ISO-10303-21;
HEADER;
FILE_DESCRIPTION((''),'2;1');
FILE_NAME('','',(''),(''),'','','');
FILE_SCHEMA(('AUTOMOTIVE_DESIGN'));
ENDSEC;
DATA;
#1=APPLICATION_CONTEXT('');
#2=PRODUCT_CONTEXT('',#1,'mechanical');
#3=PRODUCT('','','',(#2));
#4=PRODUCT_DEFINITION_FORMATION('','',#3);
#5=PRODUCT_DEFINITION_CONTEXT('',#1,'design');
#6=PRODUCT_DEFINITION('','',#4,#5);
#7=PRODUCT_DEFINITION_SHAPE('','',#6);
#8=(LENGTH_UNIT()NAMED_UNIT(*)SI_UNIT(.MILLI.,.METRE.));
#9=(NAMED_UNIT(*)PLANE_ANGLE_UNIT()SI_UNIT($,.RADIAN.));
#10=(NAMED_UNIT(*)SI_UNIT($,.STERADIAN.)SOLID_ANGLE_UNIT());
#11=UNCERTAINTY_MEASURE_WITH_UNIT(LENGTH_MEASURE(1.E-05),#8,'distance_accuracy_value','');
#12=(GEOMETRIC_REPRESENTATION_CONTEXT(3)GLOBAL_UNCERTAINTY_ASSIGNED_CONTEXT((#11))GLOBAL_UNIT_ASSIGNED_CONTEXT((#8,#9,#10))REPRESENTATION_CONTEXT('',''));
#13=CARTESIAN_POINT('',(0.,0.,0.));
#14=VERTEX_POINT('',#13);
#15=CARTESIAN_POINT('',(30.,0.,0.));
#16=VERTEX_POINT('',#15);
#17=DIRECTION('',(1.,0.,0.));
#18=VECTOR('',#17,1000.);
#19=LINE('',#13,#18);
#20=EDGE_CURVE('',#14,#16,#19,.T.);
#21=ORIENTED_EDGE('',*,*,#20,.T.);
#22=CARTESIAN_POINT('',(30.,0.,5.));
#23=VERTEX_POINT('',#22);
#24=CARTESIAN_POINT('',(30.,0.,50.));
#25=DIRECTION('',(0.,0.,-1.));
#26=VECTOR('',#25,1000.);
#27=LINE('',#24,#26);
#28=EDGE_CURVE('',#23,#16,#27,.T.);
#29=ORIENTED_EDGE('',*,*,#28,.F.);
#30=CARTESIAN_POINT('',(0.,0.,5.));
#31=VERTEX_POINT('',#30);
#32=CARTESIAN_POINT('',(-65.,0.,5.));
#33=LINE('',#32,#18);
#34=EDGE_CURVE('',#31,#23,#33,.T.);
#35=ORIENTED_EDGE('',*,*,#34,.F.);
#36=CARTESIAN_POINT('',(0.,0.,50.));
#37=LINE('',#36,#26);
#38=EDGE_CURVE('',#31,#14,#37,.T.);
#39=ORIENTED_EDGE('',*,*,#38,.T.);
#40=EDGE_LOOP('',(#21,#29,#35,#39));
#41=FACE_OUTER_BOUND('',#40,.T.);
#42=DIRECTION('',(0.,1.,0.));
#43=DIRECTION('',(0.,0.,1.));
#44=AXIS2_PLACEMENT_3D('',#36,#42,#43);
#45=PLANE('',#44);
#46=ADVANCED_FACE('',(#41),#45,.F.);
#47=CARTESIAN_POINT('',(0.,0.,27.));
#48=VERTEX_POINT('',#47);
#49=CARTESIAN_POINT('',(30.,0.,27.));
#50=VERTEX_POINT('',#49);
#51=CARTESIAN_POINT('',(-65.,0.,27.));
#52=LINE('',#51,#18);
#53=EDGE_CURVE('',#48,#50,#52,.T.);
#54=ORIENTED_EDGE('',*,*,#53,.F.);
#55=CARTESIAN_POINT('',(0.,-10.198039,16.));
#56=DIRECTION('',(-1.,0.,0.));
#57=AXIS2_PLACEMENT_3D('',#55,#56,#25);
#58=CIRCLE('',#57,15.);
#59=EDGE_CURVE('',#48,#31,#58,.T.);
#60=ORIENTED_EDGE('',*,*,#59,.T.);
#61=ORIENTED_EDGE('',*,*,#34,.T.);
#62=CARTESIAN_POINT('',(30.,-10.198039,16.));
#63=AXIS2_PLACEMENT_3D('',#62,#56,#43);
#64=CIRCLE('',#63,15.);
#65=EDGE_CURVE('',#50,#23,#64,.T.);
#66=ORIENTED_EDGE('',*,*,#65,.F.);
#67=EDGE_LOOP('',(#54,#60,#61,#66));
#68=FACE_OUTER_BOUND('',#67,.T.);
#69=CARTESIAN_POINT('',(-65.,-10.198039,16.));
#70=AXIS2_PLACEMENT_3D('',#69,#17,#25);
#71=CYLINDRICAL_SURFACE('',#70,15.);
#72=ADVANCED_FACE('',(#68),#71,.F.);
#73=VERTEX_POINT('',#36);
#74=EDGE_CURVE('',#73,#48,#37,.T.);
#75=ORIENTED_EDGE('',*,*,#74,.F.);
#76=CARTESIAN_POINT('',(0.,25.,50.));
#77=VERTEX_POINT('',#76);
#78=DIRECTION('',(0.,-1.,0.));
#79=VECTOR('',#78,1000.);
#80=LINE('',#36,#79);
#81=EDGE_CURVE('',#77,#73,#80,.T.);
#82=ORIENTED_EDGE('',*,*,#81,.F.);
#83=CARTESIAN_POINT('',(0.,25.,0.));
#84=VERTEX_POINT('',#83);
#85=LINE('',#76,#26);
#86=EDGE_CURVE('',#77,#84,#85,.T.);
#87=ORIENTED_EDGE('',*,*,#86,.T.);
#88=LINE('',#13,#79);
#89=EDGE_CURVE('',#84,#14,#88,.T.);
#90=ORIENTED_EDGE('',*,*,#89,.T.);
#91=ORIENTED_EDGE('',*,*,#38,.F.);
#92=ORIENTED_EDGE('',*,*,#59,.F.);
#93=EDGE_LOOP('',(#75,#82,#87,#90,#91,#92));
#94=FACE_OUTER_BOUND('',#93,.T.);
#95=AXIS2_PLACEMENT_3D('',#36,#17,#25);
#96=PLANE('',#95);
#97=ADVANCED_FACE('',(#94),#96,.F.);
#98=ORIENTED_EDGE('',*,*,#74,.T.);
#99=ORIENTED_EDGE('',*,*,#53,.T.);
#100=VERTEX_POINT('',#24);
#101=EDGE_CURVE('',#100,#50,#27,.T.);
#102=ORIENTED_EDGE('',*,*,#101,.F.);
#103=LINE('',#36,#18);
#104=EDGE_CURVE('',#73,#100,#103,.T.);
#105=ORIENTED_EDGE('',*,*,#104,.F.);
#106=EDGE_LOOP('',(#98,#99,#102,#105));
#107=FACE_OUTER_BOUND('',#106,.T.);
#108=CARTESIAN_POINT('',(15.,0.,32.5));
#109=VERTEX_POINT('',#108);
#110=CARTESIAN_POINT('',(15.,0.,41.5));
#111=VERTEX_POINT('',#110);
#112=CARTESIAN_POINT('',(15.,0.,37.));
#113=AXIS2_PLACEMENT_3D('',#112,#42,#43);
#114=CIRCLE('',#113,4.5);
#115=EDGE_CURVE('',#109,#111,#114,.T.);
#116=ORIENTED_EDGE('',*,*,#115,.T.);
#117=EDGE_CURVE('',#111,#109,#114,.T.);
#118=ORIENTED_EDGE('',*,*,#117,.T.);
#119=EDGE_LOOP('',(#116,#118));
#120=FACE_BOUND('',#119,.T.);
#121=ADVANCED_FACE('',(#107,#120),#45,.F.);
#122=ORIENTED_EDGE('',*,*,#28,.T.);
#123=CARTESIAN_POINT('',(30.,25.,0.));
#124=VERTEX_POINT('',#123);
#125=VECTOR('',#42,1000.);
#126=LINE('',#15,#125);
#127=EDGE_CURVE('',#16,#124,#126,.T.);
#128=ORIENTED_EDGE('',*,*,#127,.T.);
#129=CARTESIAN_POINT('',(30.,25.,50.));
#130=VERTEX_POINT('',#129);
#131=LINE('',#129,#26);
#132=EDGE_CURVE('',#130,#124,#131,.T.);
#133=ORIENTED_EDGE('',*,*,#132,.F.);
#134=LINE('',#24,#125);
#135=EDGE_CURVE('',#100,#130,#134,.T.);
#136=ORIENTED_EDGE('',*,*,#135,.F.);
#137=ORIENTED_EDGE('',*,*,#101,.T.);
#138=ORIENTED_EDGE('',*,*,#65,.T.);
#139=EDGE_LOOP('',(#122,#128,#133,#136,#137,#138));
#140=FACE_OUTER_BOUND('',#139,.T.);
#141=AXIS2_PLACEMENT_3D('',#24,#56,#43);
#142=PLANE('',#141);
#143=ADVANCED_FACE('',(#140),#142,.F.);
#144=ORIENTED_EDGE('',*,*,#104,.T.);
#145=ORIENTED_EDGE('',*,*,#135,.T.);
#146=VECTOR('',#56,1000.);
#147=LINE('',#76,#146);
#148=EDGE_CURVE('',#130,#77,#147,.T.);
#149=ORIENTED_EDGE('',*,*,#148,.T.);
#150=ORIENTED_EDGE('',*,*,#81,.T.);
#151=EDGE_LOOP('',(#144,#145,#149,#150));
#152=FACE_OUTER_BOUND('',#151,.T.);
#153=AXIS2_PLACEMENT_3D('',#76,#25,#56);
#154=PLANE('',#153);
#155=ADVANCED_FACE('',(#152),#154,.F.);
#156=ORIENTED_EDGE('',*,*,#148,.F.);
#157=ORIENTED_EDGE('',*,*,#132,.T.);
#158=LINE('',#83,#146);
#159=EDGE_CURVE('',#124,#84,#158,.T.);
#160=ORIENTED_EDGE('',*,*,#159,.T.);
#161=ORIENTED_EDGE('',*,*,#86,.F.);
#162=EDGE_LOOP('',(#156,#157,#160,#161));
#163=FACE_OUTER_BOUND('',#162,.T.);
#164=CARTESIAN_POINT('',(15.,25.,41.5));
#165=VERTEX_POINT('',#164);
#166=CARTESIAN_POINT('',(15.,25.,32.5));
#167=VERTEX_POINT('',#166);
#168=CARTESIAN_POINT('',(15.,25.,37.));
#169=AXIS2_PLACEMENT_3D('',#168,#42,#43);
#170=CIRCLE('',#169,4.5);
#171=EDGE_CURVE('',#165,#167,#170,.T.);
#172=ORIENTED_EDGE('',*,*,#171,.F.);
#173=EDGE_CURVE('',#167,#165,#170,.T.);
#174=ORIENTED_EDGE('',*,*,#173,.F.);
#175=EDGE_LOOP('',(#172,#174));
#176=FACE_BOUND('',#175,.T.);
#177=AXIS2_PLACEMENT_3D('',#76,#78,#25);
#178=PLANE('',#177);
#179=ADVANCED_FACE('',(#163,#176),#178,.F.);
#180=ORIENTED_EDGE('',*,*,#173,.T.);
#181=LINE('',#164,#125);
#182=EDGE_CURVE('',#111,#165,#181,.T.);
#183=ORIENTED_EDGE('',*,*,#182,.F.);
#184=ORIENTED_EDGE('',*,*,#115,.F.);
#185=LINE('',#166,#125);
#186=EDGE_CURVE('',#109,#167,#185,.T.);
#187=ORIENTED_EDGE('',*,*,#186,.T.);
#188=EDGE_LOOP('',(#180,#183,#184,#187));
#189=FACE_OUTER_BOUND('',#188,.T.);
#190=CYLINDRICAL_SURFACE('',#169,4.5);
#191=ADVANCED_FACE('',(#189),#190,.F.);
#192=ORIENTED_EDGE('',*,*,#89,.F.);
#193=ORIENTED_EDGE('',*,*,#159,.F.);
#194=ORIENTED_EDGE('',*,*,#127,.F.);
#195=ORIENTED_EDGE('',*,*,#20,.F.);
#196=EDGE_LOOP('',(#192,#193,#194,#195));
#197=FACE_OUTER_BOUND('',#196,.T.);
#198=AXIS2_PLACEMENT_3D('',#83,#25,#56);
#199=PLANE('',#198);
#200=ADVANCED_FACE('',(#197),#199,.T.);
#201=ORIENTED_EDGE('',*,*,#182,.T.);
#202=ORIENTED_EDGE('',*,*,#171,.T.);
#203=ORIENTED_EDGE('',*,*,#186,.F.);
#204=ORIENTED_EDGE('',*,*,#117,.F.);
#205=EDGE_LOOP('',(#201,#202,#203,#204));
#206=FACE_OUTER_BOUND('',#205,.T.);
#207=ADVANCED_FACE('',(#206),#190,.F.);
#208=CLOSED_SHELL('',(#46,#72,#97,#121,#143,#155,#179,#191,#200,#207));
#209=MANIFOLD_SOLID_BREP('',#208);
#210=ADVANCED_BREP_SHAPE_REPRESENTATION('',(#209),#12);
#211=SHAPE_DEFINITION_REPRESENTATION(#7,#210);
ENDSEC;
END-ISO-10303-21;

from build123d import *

# Parameters (mm, degrees)
SKETCH1_W              = 30
SKETCH1_H              = 25
BOSS_EXTRUDE1_DEPTH    = 50
CUT_EXTRUDE1_DEPTH     = 95
M10X1_0_TAPPED_HOLE1_D = 9


with BuildPart() as part:
    # Sketch1 → Boss-Extrude1 (new body)
    with BuildSketch(Plane.XY):
        with Locations((15, 12.5)):
            Rectangle(SKETCH1_W, SKETCH1_H)
    extrude(amount=BOSS_EXTRUDE1_DEPTH)

    # Sketch2 → Cut-Extrude1 (cut)
    with BuildSketch(Plane(origin=(30, 30, 0), x_dir=(0, -1, 0), z_dir=(-1, 0, 0))):
        with BuildLine():
            Line((30, 27), (30, 5))
            ThreePointArc((30, 5), (25.198039027, 16), (30, 27))
        make_face()
    extrude(amount=CUT_EXTRUDE1_DEPTH, mode=Mode.SUBTRACT)

    # M10x1.0 Tapped Hole1 (through all)
    with Locations(Plane(origin=(0, 25, 0), x_dir=(-1, 0, 0), z_dir=(0, 1, 0))):
        with Locations((-15, 37)):
            Hole(M10X1_0_TAPPED_HOLE1_D / 2)


solid = part.part
